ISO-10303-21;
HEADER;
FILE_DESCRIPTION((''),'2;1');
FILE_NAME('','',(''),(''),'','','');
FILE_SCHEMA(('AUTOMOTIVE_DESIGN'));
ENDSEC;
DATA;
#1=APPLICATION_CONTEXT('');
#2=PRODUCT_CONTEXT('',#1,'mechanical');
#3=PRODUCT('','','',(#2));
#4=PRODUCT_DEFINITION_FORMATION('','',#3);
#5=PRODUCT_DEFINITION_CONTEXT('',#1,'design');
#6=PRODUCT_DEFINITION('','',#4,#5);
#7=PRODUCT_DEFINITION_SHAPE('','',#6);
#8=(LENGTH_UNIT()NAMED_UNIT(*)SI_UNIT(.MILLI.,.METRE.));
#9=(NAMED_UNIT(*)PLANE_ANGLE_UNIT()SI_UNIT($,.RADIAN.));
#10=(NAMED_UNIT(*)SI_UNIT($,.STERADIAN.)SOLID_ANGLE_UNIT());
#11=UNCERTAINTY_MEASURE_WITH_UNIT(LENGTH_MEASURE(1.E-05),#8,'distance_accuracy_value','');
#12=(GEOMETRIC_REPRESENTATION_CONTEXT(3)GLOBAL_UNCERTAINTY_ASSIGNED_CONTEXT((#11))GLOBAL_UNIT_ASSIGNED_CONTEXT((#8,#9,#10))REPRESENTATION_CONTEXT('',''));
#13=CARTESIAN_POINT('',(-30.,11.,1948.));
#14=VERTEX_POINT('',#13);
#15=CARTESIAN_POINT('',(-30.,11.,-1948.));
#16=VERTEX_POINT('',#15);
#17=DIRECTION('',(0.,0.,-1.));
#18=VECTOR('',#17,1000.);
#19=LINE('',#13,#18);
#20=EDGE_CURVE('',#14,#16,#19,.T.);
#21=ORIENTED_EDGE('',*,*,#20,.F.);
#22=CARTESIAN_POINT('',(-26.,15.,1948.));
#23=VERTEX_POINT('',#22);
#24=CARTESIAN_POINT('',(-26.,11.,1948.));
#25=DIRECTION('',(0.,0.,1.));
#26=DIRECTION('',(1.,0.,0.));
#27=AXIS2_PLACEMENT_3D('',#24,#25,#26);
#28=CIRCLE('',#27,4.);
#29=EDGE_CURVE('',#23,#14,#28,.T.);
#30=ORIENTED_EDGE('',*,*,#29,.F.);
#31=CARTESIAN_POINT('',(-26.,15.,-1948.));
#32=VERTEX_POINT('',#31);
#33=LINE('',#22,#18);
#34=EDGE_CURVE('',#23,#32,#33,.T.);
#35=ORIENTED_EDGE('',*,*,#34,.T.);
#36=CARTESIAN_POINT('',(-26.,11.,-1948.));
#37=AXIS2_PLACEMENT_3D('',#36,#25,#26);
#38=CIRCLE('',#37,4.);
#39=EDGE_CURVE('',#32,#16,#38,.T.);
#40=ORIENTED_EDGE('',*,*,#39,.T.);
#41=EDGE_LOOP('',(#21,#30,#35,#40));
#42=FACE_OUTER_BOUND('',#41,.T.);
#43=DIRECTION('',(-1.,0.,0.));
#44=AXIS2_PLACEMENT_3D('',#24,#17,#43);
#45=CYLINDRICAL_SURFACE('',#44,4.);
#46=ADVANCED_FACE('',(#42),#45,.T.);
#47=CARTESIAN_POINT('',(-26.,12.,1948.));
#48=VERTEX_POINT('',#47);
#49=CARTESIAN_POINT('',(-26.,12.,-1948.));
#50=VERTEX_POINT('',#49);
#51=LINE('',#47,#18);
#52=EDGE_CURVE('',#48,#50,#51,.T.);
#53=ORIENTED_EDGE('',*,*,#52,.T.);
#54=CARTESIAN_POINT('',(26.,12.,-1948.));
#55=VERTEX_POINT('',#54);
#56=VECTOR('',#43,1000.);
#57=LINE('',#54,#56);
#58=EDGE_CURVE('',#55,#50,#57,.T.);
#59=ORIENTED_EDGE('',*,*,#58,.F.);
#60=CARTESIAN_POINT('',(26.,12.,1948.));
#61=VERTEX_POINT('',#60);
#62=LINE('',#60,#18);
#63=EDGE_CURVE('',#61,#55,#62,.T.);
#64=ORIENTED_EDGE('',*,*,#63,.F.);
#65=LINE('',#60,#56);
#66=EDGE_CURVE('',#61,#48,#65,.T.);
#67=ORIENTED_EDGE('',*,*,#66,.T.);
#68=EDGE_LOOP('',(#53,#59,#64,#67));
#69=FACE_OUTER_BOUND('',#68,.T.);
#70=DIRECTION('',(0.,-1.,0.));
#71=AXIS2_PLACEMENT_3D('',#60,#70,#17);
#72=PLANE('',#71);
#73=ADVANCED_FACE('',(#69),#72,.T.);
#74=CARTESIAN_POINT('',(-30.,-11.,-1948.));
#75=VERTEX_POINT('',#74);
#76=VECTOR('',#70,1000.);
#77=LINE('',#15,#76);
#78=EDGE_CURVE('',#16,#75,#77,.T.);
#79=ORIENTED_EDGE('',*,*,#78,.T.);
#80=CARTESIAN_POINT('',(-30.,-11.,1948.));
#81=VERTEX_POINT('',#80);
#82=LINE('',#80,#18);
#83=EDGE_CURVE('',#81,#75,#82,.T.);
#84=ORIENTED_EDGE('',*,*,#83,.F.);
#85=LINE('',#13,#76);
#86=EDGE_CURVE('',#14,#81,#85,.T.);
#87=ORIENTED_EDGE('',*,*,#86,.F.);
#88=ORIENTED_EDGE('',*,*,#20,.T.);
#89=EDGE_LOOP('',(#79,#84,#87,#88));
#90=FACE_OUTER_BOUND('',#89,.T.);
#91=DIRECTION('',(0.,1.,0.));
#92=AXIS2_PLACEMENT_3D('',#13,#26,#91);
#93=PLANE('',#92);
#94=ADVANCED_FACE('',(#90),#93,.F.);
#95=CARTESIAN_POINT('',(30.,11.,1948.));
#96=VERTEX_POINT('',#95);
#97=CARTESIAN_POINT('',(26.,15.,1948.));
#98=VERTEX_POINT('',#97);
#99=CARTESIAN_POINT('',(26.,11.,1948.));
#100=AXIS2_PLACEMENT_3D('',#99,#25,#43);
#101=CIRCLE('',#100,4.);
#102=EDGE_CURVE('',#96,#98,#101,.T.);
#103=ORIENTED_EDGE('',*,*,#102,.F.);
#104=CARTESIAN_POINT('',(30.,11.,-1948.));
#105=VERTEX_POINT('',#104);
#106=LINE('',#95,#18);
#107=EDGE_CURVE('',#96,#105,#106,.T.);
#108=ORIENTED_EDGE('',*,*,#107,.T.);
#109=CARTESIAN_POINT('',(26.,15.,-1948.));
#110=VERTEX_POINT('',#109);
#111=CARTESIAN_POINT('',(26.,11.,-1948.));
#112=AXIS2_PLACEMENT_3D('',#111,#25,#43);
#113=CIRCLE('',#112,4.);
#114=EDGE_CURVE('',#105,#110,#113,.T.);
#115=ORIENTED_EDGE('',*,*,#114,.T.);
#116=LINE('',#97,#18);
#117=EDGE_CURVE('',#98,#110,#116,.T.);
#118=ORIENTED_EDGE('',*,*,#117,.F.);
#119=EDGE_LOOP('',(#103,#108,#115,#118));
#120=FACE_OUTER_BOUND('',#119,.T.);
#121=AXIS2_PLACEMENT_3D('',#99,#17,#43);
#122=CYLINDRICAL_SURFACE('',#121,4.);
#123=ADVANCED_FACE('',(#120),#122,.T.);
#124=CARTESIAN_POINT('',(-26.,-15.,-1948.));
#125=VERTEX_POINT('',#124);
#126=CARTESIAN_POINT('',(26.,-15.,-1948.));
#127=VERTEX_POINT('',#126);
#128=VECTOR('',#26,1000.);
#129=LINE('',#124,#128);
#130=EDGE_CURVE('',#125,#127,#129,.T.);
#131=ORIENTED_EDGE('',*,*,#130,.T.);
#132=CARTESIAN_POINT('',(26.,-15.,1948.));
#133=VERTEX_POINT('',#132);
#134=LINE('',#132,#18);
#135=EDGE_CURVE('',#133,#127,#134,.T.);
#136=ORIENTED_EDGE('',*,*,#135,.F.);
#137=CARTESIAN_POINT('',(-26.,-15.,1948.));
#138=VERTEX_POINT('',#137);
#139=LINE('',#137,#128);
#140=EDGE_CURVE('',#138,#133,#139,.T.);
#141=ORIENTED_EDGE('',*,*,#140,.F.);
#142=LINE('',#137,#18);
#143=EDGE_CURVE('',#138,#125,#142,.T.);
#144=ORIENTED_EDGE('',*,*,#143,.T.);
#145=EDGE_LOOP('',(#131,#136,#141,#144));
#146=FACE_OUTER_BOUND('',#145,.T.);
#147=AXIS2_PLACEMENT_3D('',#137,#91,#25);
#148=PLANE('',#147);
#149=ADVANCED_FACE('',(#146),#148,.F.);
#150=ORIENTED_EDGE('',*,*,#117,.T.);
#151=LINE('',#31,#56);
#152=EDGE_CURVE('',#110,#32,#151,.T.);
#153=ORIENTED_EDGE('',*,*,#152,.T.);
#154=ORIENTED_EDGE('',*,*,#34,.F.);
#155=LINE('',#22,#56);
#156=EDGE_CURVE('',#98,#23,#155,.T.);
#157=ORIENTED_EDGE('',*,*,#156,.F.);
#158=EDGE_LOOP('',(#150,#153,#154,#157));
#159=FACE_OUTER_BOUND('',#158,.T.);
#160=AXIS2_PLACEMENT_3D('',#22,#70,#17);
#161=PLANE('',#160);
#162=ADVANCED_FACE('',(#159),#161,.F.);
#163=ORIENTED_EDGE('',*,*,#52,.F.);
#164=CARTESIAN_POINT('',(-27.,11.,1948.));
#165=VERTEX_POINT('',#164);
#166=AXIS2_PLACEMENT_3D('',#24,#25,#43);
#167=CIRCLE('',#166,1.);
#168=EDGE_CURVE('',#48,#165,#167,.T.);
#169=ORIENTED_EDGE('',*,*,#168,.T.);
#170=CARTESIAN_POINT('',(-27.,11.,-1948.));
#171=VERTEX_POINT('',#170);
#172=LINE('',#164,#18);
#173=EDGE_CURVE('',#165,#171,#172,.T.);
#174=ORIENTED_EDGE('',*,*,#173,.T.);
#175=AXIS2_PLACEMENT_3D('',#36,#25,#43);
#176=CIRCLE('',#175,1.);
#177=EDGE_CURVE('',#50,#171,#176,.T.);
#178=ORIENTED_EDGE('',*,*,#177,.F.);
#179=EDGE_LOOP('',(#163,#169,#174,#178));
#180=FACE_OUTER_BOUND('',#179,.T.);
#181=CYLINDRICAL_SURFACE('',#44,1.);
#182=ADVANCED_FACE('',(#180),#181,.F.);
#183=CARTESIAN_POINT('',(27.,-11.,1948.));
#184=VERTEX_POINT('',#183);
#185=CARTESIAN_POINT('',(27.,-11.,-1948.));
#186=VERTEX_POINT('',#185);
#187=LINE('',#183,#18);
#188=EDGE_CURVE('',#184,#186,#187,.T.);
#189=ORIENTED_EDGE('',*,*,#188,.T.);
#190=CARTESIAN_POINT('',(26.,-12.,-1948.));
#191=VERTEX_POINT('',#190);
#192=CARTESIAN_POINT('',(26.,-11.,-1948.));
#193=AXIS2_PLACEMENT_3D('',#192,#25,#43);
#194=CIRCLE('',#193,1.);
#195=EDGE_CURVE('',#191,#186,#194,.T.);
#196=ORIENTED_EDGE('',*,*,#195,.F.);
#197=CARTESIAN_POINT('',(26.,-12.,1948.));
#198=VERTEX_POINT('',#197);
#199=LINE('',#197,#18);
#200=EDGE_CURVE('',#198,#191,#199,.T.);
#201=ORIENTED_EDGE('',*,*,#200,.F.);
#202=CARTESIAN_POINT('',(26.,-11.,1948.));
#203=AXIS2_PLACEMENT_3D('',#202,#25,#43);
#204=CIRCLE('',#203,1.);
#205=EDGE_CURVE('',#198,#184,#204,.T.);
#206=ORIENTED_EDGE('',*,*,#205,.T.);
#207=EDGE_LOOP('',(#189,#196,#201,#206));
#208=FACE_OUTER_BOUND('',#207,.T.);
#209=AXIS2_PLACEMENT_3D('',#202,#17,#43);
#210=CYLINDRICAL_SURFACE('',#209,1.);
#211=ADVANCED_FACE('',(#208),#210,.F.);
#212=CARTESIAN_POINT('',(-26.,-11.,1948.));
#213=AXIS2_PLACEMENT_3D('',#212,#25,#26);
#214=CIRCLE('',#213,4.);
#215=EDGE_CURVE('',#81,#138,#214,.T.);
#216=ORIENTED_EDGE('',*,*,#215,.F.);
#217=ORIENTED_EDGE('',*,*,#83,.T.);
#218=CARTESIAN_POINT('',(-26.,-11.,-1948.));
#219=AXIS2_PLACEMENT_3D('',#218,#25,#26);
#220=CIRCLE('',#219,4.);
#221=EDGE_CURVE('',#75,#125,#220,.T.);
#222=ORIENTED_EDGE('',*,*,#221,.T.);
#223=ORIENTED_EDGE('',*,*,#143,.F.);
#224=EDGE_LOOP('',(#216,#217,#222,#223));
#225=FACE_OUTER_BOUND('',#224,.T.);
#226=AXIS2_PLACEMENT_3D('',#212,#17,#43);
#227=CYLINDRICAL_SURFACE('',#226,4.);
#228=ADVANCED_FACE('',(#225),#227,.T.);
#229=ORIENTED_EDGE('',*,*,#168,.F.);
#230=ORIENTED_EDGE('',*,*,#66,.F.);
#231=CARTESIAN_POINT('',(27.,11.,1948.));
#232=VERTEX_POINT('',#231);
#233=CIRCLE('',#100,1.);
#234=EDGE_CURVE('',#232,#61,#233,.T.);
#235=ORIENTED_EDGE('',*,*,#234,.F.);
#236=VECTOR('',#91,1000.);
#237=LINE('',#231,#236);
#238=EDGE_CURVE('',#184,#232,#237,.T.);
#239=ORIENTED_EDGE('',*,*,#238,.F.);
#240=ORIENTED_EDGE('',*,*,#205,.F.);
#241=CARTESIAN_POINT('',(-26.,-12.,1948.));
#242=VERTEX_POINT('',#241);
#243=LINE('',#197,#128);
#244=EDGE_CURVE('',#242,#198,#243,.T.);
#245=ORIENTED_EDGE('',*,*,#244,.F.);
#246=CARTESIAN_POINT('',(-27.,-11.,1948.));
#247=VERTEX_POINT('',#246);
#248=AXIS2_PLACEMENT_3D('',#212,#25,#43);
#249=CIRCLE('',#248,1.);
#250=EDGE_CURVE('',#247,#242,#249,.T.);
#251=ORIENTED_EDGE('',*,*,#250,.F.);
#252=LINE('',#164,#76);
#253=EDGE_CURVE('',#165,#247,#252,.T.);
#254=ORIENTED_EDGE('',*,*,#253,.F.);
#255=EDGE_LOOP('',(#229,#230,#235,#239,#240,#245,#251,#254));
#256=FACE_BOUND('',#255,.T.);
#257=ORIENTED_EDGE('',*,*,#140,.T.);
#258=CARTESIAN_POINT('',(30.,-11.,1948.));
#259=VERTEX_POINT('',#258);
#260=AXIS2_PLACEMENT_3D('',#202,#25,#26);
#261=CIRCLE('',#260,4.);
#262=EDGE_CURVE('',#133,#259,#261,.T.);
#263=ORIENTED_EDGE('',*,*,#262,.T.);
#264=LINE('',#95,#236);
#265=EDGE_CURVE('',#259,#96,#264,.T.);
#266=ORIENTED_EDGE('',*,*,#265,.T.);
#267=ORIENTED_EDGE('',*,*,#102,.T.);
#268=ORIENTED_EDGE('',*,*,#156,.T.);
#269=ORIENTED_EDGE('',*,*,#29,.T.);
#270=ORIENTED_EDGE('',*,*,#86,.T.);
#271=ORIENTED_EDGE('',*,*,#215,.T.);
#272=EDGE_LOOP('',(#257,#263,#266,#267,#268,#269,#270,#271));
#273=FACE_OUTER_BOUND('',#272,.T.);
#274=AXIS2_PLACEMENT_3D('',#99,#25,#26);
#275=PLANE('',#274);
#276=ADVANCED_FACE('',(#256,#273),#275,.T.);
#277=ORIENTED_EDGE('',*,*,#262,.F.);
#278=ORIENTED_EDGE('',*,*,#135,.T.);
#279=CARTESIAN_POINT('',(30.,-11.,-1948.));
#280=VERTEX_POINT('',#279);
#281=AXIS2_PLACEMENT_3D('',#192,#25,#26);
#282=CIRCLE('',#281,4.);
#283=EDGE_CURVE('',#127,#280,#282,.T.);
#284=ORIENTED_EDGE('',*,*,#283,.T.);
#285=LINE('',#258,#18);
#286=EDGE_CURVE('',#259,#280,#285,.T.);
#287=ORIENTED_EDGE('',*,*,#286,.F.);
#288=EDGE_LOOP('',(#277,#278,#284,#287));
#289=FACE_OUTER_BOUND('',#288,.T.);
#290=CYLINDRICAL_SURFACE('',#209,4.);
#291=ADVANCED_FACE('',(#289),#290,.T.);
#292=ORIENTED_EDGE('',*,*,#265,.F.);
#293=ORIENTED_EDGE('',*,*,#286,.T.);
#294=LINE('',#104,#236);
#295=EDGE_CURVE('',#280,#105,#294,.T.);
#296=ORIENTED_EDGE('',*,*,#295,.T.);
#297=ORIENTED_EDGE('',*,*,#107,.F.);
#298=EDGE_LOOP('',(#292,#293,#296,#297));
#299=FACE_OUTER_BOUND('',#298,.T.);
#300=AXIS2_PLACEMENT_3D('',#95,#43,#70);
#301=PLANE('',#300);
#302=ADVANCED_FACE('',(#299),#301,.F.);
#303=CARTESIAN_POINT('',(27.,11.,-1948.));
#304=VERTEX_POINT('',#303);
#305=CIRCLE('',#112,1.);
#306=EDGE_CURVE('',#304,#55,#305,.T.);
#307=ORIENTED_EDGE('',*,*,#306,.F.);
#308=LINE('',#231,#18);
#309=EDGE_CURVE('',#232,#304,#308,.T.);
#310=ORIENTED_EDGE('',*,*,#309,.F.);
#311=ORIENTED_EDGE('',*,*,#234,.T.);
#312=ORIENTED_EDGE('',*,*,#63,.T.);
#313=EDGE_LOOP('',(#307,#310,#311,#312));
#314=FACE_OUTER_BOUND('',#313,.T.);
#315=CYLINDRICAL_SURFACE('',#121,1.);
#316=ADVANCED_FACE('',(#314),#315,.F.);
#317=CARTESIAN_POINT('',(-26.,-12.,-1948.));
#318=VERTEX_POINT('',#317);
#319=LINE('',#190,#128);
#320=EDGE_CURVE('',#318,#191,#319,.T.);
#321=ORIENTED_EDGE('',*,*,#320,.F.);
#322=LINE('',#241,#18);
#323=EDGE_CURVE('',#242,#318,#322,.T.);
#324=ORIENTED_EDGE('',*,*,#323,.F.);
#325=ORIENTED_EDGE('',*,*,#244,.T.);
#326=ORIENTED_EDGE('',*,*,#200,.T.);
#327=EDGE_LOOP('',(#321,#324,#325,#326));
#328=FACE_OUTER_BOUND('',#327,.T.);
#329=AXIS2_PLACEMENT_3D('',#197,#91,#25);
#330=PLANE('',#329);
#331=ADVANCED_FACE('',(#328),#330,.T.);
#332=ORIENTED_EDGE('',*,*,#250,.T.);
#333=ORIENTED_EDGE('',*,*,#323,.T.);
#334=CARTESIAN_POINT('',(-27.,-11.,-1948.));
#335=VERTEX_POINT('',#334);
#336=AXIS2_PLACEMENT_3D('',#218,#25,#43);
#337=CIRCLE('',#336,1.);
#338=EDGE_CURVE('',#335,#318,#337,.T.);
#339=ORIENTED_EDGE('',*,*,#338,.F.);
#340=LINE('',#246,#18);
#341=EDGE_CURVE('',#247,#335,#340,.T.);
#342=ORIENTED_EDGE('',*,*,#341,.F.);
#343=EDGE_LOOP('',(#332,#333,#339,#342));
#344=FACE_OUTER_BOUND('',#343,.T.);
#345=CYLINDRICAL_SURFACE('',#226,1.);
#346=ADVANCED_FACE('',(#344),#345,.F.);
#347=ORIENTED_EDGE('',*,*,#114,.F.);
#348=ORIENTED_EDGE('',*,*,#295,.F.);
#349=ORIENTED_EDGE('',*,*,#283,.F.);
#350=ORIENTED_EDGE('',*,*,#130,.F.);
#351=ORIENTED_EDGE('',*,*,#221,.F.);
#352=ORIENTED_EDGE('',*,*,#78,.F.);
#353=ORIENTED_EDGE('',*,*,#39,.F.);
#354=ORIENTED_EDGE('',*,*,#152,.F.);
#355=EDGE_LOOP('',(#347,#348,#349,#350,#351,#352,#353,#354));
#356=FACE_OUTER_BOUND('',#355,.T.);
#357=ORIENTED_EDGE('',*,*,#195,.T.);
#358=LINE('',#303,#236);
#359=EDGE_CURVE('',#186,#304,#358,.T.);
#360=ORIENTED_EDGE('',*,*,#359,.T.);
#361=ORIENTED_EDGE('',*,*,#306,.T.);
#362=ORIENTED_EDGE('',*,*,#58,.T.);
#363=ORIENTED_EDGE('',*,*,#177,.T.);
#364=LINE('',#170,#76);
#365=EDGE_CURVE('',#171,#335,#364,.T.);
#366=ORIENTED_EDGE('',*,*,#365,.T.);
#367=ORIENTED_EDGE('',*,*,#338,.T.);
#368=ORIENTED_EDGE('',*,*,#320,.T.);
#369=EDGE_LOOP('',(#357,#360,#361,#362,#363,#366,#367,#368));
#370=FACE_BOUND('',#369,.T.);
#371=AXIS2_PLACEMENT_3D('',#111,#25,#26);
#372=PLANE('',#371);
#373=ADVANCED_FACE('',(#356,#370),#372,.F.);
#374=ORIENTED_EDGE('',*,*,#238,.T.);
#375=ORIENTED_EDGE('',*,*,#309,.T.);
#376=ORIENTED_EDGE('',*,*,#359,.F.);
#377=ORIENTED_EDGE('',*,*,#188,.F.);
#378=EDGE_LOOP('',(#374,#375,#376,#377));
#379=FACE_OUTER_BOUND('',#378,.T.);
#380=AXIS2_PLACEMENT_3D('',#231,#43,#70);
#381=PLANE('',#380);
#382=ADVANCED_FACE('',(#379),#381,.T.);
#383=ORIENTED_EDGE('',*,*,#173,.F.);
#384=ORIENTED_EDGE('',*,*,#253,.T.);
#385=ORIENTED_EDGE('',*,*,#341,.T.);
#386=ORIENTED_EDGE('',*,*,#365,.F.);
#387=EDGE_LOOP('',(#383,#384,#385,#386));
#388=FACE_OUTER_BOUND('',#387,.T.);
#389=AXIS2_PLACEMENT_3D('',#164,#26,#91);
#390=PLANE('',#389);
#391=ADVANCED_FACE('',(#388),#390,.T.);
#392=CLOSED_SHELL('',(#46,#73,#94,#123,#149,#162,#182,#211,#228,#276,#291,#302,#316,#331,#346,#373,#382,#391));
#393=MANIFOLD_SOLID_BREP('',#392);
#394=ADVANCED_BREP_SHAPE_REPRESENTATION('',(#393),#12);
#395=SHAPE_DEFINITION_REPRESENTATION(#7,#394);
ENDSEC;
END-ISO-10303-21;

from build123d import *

# Parameters (mm, degrees)
EXTRUDE_1_DEPTH = 1948


with BuildPart() as part:
    # 草图1 → 拉伸-薄壁1 (new, symmetric)
    with BuildSketch(Plane.XY):
        with BuildLine():
            Line((-26, 15), (26, 15))
            ThreePointArc((26, 15), (28.828427125, 13.828427125), (30, 11))
            Line((30, 11), (30, -11))
            ThreePointArc((30, -11), (28.828427125, -13.828427125), (26, -15))
            Line((26, -15), (-26, -15))
            ThreePointArc((-26, -15), (-28.828427125, -13.828427125), (-30, -11))
            Line((-30, -11), (-30, 11))
            ThreePointArc((-30, 11), (-28.828427125, 13.828427125), (-26, 15))
        make_face()
        with BuildLine():
            Line((-26, 12), (26, 12))
            ThreePointArc((26, 12), (26.707106781, 11.707106781), (27, 11))
            Line((27, 11), (27, -11))
            ThreePointArc((27, -11), (26.707106781, -11.707106781), (26, -12))
            Line((26, -12), (-26, -12))
            ThreePointArc((-26, -12), (-26.707106781, -11.707106781), (-27, -11))
            Line((-27, -11), (-27, 11))
            ThreePointArc((-27, 11), (-26.707106781, 11.707106781), (-26, 12))
        make_face(mode=Mode.SUBTRACT)
    extrude(amount=EXTRUDE_1_DEPTH, both=True)


solid = part.part
